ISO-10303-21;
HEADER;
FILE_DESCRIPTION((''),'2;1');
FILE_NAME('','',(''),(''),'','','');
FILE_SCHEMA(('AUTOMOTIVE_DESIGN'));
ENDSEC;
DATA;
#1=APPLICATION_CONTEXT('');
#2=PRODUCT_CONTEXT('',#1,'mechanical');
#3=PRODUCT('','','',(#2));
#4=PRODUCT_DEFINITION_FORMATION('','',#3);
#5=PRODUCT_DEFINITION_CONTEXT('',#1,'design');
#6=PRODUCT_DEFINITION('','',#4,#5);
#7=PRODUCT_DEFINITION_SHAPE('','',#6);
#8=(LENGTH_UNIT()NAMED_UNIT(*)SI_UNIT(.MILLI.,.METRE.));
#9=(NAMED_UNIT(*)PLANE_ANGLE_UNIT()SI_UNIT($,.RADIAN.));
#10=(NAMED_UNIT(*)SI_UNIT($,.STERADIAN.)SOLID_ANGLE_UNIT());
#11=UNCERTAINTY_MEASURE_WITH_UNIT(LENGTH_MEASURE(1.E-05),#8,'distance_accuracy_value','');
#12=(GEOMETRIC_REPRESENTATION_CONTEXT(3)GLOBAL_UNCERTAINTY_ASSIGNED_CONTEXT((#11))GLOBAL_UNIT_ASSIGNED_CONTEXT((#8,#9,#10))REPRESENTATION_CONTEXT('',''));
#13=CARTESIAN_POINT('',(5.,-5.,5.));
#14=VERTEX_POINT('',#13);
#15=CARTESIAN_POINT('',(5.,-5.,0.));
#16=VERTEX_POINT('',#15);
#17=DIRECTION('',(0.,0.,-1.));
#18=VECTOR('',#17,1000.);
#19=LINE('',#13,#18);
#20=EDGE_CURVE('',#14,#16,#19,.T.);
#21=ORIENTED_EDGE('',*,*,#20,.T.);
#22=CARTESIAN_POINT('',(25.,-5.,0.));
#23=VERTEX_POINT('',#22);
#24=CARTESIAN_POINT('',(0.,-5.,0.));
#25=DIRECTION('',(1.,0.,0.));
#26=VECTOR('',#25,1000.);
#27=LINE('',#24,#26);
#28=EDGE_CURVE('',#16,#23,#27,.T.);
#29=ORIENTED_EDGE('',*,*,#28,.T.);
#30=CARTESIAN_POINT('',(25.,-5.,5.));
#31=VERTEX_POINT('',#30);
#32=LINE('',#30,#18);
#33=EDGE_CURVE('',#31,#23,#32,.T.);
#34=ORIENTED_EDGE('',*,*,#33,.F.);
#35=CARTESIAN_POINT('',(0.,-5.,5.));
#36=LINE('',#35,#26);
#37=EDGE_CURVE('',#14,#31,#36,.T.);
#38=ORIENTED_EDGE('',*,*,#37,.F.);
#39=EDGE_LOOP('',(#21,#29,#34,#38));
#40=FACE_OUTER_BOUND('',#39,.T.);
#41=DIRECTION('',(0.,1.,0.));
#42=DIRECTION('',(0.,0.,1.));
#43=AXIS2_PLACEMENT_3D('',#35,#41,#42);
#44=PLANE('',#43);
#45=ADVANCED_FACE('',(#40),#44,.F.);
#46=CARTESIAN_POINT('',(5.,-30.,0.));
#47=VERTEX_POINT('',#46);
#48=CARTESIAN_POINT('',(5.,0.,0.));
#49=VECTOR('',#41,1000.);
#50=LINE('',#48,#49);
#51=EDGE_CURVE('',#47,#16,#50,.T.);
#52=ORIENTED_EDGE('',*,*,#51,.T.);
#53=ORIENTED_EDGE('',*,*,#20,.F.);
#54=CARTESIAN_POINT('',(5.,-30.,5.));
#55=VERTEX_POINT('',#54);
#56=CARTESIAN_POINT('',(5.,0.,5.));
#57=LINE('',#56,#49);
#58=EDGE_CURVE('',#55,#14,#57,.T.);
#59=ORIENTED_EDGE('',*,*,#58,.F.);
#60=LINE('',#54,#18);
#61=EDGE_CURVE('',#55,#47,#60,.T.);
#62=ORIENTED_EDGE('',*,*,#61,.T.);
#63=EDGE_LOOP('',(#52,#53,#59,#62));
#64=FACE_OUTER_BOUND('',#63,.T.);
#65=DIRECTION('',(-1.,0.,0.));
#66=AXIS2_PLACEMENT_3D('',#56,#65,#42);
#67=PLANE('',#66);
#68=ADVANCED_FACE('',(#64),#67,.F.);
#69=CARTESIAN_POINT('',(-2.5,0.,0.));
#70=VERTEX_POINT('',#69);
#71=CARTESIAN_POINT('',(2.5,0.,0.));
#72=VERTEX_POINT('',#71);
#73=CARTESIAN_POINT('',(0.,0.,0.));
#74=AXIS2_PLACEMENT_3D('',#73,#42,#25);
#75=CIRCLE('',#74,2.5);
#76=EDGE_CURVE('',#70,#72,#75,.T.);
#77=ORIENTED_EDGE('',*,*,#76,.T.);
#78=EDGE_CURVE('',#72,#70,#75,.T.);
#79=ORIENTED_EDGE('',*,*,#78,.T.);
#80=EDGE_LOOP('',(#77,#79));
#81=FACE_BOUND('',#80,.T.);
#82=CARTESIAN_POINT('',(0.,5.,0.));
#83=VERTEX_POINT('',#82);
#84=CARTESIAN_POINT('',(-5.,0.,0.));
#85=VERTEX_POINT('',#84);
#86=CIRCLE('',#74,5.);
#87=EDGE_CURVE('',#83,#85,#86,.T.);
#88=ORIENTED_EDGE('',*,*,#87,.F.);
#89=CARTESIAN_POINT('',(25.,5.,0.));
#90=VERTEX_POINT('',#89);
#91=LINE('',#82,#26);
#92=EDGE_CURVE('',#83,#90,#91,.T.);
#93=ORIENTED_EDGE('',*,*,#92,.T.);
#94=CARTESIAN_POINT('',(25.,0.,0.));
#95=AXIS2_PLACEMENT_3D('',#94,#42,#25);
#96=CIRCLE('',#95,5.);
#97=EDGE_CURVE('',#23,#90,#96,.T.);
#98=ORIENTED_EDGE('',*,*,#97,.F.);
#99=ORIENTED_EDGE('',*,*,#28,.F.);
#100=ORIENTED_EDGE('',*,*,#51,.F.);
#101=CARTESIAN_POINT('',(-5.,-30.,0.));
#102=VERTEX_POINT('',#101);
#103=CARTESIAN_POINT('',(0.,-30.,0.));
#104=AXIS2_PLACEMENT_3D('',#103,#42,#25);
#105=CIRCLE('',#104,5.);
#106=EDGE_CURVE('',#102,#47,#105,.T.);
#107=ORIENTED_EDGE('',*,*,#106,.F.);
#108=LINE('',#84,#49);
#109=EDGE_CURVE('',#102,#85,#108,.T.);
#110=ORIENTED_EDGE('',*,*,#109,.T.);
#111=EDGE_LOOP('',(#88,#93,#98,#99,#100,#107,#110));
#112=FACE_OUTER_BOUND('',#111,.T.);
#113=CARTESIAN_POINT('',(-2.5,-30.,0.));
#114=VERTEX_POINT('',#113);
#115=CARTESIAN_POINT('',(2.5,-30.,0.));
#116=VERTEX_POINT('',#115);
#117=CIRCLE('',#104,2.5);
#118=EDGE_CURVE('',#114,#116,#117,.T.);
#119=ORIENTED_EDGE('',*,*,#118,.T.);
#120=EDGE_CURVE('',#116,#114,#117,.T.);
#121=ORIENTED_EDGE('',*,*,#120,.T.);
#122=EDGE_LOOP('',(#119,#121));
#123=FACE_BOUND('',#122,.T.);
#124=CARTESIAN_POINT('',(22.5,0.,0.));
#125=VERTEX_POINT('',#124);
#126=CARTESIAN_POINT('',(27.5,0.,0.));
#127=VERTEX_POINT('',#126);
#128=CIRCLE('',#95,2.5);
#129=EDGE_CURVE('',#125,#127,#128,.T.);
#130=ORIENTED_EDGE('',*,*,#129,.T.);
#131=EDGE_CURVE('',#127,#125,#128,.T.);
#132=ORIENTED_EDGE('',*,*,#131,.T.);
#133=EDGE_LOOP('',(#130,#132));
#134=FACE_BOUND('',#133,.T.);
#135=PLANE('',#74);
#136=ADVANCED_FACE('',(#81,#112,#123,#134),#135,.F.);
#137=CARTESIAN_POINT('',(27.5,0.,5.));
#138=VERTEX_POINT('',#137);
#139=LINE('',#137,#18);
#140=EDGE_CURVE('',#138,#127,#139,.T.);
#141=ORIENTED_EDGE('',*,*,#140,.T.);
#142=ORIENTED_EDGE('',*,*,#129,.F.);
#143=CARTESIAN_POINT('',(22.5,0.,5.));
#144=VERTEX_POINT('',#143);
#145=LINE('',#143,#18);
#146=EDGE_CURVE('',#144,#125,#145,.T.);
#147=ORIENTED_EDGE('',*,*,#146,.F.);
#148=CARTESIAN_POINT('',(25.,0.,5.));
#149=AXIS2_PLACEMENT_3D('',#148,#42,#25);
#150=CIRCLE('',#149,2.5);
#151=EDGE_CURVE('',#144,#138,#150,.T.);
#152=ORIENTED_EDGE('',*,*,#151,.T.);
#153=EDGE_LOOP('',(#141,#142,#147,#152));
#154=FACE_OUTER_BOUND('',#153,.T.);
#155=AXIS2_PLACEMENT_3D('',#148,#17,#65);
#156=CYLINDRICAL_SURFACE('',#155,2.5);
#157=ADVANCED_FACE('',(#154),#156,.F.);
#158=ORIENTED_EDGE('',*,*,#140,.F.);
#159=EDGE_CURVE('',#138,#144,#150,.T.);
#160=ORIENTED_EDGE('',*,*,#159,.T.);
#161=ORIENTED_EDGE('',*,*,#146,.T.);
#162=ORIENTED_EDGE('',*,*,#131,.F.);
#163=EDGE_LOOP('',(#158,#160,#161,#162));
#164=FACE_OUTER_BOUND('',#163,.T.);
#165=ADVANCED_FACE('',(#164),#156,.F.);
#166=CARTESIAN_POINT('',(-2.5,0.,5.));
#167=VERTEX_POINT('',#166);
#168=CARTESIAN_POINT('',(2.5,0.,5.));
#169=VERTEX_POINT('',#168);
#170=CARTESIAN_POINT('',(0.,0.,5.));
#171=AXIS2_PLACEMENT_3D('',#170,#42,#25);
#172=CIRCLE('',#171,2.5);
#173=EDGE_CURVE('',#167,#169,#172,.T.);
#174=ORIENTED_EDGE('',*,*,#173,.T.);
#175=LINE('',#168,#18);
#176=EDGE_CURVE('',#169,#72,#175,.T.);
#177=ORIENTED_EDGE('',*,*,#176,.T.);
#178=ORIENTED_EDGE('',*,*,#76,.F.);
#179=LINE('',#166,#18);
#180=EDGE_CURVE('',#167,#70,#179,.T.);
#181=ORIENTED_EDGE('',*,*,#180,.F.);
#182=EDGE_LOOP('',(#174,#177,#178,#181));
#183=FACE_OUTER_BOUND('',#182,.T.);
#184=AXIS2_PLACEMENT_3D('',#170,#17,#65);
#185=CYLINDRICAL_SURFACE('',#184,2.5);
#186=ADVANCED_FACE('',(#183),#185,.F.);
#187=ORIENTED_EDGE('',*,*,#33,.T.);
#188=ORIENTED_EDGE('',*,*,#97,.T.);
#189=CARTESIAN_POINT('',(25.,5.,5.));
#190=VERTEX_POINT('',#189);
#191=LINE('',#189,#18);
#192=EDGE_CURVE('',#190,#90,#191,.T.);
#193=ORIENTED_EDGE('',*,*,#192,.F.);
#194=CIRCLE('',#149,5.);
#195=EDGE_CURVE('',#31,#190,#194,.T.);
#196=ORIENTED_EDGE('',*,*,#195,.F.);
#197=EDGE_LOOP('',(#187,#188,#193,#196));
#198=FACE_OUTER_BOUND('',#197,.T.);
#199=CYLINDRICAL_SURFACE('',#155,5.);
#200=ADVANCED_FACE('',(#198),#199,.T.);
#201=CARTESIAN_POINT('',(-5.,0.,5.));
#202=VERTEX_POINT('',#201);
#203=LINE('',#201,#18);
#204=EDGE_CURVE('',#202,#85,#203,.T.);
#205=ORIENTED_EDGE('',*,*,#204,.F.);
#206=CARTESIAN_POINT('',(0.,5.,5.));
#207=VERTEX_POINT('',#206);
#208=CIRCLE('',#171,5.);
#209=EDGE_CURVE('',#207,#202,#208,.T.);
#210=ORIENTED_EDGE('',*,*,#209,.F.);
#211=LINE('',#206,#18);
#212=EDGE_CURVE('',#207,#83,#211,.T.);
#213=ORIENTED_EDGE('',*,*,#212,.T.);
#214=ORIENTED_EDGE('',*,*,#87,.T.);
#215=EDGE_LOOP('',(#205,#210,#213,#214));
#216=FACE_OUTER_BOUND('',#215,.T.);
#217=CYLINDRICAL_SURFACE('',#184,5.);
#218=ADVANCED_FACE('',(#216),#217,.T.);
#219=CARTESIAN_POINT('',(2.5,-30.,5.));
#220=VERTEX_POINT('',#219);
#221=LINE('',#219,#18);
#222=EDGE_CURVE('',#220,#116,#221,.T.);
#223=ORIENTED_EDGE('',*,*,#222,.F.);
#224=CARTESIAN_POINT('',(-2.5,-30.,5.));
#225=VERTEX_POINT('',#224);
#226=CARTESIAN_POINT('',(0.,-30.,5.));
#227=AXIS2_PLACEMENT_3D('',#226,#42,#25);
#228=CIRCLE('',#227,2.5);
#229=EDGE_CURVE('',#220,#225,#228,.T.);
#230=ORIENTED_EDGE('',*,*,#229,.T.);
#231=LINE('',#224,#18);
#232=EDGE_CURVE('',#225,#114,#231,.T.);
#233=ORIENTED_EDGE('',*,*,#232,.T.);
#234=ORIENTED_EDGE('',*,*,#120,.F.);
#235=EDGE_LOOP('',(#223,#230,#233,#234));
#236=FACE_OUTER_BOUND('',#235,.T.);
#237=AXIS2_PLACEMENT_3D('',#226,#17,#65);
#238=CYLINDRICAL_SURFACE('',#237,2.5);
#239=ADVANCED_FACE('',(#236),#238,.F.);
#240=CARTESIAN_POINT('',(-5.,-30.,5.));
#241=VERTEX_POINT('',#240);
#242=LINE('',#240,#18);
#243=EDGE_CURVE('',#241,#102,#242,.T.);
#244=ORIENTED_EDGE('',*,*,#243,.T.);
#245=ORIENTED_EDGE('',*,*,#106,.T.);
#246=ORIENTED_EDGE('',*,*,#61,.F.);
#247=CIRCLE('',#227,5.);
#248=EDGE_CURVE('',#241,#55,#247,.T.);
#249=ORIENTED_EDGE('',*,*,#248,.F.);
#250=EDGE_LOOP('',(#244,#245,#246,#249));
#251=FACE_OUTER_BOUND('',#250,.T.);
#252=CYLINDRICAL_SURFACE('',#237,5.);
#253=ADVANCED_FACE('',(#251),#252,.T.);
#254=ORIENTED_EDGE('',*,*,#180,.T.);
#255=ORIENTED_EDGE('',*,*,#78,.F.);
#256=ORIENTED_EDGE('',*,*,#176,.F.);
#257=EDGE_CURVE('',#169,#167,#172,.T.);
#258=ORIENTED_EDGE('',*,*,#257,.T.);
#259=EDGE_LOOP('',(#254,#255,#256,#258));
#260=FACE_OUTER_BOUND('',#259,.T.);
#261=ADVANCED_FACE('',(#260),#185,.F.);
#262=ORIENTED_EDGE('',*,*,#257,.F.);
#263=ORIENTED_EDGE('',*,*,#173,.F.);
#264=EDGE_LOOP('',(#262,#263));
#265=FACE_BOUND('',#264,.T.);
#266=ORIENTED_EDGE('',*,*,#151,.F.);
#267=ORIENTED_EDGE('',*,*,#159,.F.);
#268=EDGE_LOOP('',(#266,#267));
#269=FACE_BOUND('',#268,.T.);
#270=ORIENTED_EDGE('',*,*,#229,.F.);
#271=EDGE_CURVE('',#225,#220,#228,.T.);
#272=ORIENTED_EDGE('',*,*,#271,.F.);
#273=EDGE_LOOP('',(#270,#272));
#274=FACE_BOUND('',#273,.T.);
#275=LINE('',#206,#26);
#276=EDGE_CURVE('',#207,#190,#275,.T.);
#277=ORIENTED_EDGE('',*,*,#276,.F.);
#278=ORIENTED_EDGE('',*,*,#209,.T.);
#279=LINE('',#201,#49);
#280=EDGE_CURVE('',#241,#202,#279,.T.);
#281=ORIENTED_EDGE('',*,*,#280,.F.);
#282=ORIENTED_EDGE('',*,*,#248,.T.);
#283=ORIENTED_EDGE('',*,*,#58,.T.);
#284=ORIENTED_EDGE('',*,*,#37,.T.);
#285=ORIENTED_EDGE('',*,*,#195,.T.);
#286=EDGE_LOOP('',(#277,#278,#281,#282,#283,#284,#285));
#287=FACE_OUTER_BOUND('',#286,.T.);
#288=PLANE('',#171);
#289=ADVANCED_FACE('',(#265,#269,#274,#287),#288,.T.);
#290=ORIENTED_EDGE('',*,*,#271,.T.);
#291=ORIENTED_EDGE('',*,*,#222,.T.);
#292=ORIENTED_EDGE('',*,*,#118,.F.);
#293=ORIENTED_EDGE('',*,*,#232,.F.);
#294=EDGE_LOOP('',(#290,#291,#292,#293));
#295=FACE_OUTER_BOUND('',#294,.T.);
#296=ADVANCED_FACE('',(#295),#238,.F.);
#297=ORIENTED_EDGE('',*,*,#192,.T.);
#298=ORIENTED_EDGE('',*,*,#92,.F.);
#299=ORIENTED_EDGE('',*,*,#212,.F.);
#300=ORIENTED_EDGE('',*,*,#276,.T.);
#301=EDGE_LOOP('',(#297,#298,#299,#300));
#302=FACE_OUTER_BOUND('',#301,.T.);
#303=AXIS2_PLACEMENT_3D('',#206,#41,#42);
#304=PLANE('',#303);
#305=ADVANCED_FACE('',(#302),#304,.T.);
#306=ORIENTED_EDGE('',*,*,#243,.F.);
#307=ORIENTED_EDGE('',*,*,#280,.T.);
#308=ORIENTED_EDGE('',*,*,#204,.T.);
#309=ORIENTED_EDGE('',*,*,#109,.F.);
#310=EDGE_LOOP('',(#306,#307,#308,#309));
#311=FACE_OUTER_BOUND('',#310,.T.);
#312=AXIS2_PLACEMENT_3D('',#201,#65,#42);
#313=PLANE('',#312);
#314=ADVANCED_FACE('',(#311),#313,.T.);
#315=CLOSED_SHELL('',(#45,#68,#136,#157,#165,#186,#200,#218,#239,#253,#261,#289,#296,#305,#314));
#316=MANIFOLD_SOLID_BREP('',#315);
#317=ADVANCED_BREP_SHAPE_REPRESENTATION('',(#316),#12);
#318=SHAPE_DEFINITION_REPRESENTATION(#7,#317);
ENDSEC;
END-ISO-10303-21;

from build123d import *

# Parameters (mm, degrees)
L_LINK_PROFILE_R       = 2.5
L_LINK_PLATE_5MM_DEPTH = 5


with BuildPart() as part:
    # L-Link Profile → L-Link Plate 5mm (new body)
    # profile 1 of 3: a face of its own
    with BuildSketch(Plane.XY):
        with BuildLine():
            Line((25, 5), (0, 5))
            ThreePointArc((0, 5), (3.535533906, 3.535533906), (5, 0))
            Line((5, 0), (5, -5))
            Line((5, -5), (25, -5))
            ThreePointArc((25, -5), (30, 0), (25, 5))
        make_face()
        with Locations((25, 0)):
            Circle(L_LINK_PROFILE_R, mode=Mode.SUBTRACT)
    # profile 2 of 3: a face of its own
    with BuildSketch(Plane.XY):
        with BuildLine():
            Line((-5, 0), (-5, -30))
            ThreePointArc((-5, -30), (0, -35), (5, -30))
            Line((5, -30), (5, -5))
            Line((5, -5), (0, -5))
            ThreePointArc((0, -5), (-3.535533906, -3.535533906), (-5, 0))
        make_face()
        with Locations((0, -30)):
            Circle(L_LINK_PROFILE_R, mode=Mode.SUBTRACT)
    # profile 3 of 3: a face of its own
    with BuildSketch(Plane.XY):
        with BuildLine():
            ThreePointArc((0, 5), (-3.535533906, 3.535533906), (-5, 0))
            ThreePointArc((-5, 0), (-3.535533906, -3.535533906), (0, -5))
            Line((0, -5), (5, -5))
            Line((5, -5), (5, 0))
            ThreePointArc((5, 0), (3.535533906, 3.535533906), (0, 5))
        make_face()
        Circle(L_LINK_PROFILE_R, mode=Mode.SUBTRACT)
    extrude(amount=L_LINK_PLATE_5MM_DEPTH)


solid = part.part
